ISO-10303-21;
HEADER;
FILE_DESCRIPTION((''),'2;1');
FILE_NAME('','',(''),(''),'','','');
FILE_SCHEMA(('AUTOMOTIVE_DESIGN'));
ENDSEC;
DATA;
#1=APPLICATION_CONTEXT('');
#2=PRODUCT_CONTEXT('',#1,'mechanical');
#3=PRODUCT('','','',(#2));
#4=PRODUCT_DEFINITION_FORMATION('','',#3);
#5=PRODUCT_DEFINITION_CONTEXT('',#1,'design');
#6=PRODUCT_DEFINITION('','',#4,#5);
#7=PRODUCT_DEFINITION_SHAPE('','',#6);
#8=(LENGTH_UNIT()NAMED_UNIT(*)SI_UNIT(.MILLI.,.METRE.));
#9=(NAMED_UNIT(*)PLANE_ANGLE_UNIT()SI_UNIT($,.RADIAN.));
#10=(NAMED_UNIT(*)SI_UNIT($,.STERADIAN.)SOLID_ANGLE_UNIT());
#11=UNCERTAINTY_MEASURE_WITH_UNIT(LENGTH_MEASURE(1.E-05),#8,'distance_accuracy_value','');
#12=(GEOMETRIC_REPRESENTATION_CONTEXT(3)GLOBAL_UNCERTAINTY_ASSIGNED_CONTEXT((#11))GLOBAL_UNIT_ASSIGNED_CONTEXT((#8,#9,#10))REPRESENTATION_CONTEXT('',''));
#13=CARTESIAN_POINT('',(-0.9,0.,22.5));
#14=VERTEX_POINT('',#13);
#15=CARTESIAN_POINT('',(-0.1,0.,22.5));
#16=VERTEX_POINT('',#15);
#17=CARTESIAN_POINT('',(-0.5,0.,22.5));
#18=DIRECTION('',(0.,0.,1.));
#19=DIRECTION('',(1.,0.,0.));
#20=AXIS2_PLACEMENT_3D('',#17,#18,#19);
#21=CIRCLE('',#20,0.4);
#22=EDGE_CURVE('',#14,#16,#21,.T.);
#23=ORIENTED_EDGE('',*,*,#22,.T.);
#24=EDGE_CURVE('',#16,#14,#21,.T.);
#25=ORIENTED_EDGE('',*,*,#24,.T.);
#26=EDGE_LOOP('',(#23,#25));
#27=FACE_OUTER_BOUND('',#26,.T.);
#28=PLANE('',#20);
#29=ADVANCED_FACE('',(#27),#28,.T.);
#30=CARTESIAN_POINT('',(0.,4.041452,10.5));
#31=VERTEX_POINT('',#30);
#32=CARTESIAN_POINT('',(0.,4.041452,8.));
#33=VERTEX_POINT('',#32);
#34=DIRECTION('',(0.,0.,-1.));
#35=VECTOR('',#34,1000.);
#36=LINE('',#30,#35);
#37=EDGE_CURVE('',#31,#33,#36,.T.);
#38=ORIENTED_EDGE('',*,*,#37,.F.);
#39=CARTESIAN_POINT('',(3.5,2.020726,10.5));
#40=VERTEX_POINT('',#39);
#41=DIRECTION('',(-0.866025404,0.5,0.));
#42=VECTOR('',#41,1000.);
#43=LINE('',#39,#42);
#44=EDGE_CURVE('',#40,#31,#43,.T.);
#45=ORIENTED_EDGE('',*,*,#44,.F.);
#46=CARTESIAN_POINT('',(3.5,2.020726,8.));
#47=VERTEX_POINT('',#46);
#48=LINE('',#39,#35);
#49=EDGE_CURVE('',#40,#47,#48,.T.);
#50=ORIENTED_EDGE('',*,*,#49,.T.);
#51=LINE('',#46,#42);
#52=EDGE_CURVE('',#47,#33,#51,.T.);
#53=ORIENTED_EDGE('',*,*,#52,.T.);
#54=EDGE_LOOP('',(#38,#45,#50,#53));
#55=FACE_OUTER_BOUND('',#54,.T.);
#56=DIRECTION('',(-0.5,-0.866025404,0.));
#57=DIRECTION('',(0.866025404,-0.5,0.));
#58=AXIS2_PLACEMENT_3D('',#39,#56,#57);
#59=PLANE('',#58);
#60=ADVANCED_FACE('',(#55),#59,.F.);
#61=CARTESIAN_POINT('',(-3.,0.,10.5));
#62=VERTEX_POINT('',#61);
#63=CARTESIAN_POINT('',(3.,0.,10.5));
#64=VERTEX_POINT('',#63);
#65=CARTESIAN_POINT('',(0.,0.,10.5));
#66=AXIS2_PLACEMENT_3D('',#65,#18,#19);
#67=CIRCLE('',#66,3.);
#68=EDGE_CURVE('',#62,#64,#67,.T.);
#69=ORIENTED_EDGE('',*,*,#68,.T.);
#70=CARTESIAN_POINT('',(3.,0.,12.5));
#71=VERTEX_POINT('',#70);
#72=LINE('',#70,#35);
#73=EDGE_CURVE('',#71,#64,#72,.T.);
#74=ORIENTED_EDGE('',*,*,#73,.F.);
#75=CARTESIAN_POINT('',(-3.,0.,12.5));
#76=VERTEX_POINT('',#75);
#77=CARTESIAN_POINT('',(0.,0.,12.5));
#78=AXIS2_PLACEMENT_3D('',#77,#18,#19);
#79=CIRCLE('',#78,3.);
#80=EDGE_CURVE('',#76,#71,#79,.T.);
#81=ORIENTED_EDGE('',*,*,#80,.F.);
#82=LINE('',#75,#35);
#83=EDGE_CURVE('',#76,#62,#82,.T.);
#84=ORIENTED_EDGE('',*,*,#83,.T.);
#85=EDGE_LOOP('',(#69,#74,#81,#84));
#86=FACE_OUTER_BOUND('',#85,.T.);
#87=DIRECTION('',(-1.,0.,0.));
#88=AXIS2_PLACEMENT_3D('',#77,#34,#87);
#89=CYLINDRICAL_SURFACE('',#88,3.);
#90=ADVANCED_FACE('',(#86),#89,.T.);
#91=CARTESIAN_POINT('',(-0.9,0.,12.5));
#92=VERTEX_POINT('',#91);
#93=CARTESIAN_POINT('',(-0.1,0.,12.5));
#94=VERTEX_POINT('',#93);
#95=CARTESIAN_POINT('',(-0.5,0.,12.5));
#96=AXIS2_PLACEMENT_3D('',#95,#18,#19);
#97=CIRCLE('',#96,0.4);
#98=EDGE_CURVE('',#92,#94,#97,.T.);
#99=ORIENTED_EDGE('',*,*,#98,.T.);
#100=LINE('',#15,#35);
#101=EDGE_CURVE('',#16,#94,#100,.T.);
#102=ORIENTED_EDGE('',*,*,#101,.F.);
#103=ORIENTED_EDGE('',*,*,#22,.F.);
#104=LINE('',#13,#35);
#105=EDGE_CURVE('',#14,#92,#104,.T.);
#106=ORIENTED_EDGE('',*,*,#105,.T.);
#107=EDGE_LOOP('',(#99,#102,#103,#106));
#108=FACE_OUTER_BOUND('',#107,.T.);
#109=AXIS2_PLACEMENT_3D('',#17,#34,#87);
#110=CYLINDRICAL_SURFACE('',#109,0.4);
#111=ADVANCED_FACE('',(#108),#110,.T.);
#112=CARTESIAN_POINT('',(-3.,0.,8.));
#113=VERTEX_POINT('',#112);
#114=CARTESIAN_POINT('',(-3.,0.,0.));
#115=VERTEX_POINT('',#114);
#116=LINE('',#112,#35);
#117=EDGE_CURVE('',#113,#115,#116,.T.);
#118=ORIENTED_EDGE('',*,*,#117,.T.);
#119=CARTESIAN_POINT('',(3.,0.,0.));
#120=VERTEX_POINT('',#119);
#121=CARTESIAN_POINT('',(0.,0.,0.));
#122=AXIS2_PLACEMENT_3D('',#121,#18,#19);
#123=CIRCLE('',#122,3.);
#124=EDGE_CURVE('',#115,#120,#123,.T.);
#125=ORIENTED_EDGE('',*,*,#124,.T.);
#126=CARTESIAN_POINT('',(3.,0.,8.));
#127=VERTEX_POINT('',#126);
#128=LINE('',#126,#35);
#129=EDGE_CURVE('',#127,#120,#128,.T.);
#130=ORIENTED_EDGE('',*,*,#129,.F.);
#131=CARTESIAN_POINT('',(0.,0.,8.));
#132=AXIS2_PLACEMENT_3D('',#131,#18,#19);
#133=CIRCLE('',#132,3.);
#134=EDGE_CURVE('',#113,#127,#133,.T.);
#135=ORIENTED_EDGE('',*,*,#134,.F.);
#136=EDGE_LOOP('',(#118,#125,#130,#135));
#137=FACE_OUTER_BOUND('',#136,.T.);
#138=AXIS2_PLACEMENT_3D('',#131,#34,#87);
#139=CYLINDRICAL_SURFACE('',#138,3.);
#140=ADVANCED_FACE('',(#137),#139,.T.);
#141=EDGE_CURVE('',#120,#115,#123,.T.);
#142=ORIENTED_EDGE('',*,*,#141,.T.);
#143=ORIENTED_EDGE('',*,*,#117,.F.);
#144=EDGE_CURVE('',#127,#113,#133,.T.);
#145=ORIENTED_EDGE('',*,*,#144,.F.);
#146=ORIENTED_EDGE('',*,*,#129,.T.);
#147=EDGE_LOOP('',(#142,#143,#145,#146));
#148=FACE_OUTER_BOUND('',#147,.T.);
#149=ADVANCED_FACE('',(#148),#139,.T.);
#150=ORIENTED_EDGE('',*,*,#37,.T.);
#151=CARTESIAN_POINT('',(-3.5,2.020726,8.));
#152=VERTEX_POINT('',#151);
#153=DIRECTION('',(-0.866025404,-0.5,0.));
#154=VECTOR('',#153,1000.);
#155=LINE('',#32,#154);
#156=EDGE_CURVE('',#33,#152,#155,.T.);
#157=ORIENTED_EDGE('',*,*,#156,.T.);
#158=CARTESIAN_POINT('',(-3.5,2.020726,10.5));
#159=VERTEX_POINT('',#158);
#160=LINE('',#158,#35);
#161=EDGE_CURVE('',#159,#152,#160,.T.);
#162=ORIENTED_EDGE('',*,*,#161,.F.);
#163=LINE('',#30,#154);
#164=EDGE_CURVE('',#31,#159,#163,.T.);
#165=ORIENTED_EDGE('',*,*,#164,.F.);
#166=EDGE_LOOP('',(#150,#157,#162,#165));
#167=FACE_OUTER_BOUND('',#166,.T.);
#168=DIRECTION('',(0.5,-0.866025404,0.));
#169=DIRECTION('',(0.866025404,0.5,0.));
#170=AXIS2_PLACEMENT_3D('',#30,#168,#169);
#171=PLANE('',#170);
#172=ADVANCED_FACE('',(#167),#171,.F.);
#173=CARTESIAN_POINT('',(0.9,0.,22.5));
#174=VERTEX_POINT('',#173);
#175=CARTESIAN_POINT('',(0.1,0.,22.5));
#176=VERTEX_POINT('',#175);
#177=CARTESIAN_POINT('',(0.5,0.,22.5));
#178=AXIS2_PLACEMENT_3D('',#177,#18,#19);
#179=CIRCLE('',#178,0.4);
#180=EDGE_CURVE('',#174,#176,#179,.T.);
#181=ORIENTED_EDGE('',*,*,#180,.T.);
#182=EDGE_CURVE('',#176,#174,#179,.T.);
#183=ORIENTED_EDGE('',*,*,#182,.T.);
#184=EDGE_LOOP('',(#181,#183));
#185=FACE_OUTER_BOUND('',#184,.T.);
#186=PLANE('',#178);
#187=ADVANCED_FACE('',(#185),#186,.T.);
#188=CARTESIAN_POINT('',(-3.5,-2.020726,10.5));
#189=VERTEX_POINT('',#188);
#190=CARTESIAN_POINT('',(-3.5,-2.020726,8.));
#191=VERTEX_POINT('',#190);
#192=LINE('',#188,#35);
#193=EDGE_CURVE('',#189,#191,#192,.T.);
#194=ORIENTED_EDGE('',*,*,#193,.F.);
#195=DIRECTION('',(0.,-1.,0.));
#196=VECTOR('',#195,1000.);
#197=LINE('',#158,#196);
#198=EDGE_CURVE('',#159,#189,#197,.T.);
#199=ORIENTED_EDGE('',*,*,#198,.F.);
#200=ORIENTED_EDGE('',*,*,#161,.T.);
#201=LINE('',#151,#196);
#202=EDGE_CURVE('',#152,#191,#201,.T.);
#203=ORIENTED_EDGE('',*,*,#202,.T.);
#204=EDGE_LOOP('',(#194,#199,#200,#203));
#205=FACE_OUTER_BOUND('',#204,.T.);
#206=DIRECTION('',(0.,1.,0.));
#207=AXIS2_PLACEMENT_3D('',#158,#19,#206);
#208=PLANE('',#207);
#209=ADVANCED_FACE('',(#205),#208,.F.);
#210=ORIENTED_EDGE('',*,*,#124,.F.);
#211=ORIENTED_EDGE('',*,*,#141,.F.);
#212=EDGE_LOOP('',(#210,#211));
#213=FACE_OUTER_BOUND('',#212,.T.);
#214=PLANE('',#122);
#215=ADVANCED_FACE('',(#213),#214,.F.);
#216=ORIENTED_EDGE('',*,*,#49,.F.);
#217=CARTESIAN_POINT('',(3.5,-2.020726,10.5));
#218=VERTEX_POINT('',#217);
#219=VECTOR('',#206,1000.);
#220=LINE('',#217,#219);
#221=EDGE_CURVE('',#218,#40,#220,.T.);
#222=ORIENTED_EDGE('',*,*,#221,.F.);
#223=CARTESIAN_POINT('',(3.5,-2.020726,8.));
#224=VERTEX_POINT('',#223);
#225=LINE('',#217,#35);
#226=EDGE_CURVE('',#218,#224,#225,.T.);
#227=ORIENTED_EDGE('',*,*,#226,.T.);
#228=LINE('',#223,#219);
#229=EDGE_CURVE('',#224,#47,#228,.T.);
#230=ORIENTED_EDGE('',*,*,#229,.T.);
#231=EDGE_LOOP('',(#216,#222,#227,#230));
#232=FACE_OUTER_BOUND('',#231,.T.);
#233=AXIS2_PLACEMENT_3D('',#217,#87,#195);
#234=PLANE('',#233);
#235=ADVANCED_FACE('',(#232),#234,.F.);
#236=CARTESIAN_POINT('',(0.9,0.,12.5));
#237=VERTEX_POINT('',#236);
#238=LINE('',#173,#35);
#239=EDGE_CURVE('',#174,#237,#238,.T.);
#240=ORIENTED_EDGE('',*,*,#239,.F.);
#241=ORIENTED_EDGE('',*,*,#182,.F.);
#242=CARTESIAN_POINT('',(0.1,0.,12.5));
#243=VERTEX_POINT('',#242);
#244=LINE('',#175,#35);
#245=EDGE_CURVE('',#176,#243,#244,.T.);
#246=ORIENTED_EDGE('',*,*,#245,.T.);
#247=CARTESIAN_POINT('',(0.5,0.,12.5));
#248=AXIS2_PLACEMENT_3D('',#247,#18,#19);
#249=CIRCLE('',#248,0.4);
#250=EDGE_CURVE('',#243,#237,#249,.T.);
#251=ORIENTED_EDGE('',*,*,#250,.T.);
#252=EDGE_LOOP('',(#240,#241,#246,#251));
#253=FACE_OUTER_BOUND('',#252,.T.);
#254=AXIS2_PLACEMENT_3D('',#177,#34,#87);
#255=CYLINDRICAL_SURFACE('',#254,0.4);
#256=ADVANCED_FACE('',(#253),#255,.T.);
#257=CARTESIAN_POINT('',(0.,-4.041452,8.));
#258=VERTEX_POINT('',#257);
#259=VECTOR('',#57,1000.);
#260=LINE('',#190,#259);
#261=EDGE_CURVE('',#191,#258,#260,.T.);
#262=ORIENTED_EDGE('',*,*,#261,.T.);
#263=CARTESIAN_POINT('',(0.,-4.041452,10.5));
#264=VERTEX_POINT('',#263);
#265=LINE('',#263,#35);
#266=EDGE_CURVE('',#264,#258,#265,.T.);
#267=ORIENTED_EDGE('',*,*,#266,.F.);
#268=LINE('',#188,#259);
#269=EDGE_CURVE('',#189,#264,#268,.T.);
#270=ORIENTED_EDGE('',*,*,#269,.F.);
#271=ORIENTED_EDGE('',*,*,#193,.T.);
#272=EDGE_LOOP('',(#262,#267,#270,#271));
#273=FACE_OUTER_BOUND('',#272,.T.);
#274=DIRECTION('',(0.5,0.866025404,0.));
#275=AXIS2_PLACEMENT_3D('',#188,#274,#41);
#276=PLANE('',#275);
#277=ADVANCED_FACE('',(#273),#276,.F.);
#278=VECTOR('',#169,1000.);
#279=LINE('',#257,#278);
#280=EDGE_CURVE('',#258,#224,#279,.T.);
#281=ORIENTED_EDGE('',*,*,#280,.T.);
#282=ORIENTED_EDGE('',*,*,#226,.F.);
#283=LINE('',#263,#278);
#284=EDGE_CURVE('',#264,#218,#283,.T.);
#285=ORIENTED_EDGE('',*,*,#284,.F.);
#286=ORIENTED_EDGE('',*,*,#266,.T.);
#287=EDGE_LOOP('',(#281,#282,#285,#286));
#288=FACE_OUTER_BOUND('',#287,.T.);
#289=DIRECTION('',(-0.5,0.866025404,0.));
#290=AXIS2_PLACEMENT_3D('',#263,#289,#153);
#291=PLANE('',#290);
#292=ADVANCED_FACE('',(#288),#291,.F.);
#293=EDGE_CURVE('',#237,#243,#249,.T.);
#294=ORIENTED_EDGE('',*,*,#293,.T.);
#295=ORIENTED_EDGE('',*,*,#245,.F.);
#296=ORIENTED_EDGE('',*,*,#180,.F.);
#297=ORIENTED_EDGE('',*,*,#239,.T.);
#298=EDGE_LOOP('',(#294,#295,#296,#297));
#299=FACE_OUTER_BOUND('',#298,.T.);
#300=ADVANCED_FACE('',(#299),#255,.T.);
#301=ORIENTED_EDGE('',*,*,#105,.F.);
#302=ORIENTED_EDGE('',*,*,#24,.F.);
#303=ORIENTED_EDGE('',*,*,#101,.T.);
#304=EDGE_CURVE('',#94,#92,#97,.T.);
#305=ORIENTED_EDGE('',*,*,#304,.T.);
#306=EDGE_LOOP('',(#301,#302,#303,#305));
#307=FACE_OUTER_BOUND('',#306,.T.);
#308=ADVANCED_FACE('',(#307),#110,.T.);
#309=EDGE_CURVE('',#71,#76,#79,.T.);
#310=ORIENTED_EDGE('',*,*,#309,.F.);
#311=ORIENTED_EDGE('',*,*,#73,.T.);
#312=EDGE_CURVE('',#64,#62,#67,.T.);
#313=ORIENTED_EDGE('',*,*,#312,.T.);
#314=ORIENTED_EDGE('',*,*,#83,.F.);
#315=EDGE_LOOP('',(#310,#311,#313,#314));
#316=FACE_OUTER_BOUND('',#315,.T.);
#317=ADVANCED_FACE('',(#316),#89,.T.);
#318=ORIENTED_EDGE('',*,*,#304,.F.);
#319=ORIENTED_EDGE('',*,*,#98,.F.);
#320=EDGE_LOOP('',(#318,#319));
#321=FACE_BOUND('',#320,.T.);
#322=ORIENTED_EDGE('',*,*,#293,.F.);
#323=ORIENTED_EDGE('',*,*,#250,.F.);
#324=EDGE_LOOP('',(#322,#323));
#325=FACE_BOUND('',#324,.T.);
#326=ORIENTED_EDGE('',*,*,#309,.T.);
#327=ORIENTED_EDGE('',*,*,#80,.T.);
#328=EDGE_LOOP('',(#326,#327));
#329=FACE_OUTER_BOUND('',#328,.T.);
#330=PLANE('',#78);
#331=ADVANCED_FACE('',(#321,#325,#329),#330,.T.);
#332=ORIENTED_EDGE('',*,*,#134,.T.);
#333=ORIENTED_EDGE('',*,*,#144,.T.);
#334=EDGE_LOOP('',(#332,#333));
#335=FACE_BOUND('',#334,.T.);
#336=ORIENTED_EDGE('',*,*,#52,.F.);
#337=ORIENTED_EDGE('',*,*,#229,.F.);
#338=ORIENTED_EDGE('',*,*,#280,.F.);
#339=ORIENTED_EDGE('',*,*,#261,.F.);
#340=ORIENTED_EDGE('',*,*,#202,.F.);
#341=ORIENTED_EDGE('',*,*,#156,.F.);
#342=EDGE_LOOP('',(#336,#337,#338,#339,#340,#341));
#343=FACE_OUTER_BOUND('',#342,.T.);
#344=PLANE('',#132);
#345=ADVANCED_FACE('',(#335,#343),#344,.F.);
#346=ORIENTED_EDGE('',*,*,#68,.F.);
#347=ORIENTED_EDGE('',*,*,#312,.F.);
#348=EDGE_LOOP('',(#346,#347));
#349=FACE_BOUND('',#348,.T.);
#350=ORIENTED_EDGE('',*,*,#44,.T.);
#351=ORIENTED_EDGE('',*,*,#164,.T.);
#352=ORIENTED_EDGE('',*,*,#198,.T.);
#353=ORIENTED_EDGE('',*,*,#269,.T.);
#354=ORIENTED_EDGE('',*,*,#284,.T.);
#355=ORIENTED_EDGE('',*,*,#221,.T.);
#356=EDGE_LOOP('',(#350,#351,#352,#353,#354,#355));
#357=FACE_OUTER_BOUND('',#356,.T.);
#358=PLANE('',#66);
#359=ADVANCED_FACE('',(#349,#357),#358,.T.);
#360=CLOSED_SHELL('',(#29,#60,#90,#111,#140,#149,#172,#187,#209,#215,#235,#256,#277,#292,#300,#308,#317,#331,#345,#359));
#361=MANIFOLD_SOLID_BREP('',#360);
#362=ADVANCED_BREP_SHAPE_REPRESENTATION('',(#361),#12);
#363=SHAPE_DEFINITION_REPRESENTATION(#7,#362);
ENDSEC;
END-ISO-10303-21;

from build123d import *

# Parameters (mm, degrees)
SKETCH1_R           = 3
BOSS_EXTRUDE1_DEPTH = 8
BOSS_EXTRUDE2_DEPTH = 2.5
SKETCH3_R           = 3
BOSS_EXTRUDE3_DEPTH = 2
SKETCH4_R           = 0.4
BOSS_EXTRUDE4_DEPTH = 10


with BuildPart() as part:
    # Sketch1 → Boss-Extrude1 (new body)
    with BuildSketch(Plane.XY):
        Circle(SKETCH1_R)
    extrude(amount=BOSS_EXTRUDE1_DEPTH)

    # Sketch2 → Boss-Extrude2 (add)
    with BuildSketch(Plane.XY.offset(8)):
        Polygon((0, 4.041451884), (-3.5, 2.020725942), (-3.5, -2.020725942), (0, -4.041451884), (3.5, -2.020725942), (3.5, 2.020725942), align=None)
    extrude(amount=BOSS_EXTRUDE2_DEPTH)

    # Sketch3 → Boss-Extrude3 (add)
    with BuildSketch(Plane.XY.offset(10.5)):
        Circle(SKETCH3_R)
    extrude(amount=BOSS_EXTRUDE3_DEPTH)

    # Sketch4 → Boss-Extrude4 (add)
    with BuildSketch(Plane.XY.offset(12.5)):
        with Locations((0.5, 0)):
            Circle(SKETCH4_R)
        with Locations((-0.5, 0)):
            Circle(SKETCH4_R)
    extrude(amount=BOSS_EXTRUDE4_DEPTH)


solid = part.part
